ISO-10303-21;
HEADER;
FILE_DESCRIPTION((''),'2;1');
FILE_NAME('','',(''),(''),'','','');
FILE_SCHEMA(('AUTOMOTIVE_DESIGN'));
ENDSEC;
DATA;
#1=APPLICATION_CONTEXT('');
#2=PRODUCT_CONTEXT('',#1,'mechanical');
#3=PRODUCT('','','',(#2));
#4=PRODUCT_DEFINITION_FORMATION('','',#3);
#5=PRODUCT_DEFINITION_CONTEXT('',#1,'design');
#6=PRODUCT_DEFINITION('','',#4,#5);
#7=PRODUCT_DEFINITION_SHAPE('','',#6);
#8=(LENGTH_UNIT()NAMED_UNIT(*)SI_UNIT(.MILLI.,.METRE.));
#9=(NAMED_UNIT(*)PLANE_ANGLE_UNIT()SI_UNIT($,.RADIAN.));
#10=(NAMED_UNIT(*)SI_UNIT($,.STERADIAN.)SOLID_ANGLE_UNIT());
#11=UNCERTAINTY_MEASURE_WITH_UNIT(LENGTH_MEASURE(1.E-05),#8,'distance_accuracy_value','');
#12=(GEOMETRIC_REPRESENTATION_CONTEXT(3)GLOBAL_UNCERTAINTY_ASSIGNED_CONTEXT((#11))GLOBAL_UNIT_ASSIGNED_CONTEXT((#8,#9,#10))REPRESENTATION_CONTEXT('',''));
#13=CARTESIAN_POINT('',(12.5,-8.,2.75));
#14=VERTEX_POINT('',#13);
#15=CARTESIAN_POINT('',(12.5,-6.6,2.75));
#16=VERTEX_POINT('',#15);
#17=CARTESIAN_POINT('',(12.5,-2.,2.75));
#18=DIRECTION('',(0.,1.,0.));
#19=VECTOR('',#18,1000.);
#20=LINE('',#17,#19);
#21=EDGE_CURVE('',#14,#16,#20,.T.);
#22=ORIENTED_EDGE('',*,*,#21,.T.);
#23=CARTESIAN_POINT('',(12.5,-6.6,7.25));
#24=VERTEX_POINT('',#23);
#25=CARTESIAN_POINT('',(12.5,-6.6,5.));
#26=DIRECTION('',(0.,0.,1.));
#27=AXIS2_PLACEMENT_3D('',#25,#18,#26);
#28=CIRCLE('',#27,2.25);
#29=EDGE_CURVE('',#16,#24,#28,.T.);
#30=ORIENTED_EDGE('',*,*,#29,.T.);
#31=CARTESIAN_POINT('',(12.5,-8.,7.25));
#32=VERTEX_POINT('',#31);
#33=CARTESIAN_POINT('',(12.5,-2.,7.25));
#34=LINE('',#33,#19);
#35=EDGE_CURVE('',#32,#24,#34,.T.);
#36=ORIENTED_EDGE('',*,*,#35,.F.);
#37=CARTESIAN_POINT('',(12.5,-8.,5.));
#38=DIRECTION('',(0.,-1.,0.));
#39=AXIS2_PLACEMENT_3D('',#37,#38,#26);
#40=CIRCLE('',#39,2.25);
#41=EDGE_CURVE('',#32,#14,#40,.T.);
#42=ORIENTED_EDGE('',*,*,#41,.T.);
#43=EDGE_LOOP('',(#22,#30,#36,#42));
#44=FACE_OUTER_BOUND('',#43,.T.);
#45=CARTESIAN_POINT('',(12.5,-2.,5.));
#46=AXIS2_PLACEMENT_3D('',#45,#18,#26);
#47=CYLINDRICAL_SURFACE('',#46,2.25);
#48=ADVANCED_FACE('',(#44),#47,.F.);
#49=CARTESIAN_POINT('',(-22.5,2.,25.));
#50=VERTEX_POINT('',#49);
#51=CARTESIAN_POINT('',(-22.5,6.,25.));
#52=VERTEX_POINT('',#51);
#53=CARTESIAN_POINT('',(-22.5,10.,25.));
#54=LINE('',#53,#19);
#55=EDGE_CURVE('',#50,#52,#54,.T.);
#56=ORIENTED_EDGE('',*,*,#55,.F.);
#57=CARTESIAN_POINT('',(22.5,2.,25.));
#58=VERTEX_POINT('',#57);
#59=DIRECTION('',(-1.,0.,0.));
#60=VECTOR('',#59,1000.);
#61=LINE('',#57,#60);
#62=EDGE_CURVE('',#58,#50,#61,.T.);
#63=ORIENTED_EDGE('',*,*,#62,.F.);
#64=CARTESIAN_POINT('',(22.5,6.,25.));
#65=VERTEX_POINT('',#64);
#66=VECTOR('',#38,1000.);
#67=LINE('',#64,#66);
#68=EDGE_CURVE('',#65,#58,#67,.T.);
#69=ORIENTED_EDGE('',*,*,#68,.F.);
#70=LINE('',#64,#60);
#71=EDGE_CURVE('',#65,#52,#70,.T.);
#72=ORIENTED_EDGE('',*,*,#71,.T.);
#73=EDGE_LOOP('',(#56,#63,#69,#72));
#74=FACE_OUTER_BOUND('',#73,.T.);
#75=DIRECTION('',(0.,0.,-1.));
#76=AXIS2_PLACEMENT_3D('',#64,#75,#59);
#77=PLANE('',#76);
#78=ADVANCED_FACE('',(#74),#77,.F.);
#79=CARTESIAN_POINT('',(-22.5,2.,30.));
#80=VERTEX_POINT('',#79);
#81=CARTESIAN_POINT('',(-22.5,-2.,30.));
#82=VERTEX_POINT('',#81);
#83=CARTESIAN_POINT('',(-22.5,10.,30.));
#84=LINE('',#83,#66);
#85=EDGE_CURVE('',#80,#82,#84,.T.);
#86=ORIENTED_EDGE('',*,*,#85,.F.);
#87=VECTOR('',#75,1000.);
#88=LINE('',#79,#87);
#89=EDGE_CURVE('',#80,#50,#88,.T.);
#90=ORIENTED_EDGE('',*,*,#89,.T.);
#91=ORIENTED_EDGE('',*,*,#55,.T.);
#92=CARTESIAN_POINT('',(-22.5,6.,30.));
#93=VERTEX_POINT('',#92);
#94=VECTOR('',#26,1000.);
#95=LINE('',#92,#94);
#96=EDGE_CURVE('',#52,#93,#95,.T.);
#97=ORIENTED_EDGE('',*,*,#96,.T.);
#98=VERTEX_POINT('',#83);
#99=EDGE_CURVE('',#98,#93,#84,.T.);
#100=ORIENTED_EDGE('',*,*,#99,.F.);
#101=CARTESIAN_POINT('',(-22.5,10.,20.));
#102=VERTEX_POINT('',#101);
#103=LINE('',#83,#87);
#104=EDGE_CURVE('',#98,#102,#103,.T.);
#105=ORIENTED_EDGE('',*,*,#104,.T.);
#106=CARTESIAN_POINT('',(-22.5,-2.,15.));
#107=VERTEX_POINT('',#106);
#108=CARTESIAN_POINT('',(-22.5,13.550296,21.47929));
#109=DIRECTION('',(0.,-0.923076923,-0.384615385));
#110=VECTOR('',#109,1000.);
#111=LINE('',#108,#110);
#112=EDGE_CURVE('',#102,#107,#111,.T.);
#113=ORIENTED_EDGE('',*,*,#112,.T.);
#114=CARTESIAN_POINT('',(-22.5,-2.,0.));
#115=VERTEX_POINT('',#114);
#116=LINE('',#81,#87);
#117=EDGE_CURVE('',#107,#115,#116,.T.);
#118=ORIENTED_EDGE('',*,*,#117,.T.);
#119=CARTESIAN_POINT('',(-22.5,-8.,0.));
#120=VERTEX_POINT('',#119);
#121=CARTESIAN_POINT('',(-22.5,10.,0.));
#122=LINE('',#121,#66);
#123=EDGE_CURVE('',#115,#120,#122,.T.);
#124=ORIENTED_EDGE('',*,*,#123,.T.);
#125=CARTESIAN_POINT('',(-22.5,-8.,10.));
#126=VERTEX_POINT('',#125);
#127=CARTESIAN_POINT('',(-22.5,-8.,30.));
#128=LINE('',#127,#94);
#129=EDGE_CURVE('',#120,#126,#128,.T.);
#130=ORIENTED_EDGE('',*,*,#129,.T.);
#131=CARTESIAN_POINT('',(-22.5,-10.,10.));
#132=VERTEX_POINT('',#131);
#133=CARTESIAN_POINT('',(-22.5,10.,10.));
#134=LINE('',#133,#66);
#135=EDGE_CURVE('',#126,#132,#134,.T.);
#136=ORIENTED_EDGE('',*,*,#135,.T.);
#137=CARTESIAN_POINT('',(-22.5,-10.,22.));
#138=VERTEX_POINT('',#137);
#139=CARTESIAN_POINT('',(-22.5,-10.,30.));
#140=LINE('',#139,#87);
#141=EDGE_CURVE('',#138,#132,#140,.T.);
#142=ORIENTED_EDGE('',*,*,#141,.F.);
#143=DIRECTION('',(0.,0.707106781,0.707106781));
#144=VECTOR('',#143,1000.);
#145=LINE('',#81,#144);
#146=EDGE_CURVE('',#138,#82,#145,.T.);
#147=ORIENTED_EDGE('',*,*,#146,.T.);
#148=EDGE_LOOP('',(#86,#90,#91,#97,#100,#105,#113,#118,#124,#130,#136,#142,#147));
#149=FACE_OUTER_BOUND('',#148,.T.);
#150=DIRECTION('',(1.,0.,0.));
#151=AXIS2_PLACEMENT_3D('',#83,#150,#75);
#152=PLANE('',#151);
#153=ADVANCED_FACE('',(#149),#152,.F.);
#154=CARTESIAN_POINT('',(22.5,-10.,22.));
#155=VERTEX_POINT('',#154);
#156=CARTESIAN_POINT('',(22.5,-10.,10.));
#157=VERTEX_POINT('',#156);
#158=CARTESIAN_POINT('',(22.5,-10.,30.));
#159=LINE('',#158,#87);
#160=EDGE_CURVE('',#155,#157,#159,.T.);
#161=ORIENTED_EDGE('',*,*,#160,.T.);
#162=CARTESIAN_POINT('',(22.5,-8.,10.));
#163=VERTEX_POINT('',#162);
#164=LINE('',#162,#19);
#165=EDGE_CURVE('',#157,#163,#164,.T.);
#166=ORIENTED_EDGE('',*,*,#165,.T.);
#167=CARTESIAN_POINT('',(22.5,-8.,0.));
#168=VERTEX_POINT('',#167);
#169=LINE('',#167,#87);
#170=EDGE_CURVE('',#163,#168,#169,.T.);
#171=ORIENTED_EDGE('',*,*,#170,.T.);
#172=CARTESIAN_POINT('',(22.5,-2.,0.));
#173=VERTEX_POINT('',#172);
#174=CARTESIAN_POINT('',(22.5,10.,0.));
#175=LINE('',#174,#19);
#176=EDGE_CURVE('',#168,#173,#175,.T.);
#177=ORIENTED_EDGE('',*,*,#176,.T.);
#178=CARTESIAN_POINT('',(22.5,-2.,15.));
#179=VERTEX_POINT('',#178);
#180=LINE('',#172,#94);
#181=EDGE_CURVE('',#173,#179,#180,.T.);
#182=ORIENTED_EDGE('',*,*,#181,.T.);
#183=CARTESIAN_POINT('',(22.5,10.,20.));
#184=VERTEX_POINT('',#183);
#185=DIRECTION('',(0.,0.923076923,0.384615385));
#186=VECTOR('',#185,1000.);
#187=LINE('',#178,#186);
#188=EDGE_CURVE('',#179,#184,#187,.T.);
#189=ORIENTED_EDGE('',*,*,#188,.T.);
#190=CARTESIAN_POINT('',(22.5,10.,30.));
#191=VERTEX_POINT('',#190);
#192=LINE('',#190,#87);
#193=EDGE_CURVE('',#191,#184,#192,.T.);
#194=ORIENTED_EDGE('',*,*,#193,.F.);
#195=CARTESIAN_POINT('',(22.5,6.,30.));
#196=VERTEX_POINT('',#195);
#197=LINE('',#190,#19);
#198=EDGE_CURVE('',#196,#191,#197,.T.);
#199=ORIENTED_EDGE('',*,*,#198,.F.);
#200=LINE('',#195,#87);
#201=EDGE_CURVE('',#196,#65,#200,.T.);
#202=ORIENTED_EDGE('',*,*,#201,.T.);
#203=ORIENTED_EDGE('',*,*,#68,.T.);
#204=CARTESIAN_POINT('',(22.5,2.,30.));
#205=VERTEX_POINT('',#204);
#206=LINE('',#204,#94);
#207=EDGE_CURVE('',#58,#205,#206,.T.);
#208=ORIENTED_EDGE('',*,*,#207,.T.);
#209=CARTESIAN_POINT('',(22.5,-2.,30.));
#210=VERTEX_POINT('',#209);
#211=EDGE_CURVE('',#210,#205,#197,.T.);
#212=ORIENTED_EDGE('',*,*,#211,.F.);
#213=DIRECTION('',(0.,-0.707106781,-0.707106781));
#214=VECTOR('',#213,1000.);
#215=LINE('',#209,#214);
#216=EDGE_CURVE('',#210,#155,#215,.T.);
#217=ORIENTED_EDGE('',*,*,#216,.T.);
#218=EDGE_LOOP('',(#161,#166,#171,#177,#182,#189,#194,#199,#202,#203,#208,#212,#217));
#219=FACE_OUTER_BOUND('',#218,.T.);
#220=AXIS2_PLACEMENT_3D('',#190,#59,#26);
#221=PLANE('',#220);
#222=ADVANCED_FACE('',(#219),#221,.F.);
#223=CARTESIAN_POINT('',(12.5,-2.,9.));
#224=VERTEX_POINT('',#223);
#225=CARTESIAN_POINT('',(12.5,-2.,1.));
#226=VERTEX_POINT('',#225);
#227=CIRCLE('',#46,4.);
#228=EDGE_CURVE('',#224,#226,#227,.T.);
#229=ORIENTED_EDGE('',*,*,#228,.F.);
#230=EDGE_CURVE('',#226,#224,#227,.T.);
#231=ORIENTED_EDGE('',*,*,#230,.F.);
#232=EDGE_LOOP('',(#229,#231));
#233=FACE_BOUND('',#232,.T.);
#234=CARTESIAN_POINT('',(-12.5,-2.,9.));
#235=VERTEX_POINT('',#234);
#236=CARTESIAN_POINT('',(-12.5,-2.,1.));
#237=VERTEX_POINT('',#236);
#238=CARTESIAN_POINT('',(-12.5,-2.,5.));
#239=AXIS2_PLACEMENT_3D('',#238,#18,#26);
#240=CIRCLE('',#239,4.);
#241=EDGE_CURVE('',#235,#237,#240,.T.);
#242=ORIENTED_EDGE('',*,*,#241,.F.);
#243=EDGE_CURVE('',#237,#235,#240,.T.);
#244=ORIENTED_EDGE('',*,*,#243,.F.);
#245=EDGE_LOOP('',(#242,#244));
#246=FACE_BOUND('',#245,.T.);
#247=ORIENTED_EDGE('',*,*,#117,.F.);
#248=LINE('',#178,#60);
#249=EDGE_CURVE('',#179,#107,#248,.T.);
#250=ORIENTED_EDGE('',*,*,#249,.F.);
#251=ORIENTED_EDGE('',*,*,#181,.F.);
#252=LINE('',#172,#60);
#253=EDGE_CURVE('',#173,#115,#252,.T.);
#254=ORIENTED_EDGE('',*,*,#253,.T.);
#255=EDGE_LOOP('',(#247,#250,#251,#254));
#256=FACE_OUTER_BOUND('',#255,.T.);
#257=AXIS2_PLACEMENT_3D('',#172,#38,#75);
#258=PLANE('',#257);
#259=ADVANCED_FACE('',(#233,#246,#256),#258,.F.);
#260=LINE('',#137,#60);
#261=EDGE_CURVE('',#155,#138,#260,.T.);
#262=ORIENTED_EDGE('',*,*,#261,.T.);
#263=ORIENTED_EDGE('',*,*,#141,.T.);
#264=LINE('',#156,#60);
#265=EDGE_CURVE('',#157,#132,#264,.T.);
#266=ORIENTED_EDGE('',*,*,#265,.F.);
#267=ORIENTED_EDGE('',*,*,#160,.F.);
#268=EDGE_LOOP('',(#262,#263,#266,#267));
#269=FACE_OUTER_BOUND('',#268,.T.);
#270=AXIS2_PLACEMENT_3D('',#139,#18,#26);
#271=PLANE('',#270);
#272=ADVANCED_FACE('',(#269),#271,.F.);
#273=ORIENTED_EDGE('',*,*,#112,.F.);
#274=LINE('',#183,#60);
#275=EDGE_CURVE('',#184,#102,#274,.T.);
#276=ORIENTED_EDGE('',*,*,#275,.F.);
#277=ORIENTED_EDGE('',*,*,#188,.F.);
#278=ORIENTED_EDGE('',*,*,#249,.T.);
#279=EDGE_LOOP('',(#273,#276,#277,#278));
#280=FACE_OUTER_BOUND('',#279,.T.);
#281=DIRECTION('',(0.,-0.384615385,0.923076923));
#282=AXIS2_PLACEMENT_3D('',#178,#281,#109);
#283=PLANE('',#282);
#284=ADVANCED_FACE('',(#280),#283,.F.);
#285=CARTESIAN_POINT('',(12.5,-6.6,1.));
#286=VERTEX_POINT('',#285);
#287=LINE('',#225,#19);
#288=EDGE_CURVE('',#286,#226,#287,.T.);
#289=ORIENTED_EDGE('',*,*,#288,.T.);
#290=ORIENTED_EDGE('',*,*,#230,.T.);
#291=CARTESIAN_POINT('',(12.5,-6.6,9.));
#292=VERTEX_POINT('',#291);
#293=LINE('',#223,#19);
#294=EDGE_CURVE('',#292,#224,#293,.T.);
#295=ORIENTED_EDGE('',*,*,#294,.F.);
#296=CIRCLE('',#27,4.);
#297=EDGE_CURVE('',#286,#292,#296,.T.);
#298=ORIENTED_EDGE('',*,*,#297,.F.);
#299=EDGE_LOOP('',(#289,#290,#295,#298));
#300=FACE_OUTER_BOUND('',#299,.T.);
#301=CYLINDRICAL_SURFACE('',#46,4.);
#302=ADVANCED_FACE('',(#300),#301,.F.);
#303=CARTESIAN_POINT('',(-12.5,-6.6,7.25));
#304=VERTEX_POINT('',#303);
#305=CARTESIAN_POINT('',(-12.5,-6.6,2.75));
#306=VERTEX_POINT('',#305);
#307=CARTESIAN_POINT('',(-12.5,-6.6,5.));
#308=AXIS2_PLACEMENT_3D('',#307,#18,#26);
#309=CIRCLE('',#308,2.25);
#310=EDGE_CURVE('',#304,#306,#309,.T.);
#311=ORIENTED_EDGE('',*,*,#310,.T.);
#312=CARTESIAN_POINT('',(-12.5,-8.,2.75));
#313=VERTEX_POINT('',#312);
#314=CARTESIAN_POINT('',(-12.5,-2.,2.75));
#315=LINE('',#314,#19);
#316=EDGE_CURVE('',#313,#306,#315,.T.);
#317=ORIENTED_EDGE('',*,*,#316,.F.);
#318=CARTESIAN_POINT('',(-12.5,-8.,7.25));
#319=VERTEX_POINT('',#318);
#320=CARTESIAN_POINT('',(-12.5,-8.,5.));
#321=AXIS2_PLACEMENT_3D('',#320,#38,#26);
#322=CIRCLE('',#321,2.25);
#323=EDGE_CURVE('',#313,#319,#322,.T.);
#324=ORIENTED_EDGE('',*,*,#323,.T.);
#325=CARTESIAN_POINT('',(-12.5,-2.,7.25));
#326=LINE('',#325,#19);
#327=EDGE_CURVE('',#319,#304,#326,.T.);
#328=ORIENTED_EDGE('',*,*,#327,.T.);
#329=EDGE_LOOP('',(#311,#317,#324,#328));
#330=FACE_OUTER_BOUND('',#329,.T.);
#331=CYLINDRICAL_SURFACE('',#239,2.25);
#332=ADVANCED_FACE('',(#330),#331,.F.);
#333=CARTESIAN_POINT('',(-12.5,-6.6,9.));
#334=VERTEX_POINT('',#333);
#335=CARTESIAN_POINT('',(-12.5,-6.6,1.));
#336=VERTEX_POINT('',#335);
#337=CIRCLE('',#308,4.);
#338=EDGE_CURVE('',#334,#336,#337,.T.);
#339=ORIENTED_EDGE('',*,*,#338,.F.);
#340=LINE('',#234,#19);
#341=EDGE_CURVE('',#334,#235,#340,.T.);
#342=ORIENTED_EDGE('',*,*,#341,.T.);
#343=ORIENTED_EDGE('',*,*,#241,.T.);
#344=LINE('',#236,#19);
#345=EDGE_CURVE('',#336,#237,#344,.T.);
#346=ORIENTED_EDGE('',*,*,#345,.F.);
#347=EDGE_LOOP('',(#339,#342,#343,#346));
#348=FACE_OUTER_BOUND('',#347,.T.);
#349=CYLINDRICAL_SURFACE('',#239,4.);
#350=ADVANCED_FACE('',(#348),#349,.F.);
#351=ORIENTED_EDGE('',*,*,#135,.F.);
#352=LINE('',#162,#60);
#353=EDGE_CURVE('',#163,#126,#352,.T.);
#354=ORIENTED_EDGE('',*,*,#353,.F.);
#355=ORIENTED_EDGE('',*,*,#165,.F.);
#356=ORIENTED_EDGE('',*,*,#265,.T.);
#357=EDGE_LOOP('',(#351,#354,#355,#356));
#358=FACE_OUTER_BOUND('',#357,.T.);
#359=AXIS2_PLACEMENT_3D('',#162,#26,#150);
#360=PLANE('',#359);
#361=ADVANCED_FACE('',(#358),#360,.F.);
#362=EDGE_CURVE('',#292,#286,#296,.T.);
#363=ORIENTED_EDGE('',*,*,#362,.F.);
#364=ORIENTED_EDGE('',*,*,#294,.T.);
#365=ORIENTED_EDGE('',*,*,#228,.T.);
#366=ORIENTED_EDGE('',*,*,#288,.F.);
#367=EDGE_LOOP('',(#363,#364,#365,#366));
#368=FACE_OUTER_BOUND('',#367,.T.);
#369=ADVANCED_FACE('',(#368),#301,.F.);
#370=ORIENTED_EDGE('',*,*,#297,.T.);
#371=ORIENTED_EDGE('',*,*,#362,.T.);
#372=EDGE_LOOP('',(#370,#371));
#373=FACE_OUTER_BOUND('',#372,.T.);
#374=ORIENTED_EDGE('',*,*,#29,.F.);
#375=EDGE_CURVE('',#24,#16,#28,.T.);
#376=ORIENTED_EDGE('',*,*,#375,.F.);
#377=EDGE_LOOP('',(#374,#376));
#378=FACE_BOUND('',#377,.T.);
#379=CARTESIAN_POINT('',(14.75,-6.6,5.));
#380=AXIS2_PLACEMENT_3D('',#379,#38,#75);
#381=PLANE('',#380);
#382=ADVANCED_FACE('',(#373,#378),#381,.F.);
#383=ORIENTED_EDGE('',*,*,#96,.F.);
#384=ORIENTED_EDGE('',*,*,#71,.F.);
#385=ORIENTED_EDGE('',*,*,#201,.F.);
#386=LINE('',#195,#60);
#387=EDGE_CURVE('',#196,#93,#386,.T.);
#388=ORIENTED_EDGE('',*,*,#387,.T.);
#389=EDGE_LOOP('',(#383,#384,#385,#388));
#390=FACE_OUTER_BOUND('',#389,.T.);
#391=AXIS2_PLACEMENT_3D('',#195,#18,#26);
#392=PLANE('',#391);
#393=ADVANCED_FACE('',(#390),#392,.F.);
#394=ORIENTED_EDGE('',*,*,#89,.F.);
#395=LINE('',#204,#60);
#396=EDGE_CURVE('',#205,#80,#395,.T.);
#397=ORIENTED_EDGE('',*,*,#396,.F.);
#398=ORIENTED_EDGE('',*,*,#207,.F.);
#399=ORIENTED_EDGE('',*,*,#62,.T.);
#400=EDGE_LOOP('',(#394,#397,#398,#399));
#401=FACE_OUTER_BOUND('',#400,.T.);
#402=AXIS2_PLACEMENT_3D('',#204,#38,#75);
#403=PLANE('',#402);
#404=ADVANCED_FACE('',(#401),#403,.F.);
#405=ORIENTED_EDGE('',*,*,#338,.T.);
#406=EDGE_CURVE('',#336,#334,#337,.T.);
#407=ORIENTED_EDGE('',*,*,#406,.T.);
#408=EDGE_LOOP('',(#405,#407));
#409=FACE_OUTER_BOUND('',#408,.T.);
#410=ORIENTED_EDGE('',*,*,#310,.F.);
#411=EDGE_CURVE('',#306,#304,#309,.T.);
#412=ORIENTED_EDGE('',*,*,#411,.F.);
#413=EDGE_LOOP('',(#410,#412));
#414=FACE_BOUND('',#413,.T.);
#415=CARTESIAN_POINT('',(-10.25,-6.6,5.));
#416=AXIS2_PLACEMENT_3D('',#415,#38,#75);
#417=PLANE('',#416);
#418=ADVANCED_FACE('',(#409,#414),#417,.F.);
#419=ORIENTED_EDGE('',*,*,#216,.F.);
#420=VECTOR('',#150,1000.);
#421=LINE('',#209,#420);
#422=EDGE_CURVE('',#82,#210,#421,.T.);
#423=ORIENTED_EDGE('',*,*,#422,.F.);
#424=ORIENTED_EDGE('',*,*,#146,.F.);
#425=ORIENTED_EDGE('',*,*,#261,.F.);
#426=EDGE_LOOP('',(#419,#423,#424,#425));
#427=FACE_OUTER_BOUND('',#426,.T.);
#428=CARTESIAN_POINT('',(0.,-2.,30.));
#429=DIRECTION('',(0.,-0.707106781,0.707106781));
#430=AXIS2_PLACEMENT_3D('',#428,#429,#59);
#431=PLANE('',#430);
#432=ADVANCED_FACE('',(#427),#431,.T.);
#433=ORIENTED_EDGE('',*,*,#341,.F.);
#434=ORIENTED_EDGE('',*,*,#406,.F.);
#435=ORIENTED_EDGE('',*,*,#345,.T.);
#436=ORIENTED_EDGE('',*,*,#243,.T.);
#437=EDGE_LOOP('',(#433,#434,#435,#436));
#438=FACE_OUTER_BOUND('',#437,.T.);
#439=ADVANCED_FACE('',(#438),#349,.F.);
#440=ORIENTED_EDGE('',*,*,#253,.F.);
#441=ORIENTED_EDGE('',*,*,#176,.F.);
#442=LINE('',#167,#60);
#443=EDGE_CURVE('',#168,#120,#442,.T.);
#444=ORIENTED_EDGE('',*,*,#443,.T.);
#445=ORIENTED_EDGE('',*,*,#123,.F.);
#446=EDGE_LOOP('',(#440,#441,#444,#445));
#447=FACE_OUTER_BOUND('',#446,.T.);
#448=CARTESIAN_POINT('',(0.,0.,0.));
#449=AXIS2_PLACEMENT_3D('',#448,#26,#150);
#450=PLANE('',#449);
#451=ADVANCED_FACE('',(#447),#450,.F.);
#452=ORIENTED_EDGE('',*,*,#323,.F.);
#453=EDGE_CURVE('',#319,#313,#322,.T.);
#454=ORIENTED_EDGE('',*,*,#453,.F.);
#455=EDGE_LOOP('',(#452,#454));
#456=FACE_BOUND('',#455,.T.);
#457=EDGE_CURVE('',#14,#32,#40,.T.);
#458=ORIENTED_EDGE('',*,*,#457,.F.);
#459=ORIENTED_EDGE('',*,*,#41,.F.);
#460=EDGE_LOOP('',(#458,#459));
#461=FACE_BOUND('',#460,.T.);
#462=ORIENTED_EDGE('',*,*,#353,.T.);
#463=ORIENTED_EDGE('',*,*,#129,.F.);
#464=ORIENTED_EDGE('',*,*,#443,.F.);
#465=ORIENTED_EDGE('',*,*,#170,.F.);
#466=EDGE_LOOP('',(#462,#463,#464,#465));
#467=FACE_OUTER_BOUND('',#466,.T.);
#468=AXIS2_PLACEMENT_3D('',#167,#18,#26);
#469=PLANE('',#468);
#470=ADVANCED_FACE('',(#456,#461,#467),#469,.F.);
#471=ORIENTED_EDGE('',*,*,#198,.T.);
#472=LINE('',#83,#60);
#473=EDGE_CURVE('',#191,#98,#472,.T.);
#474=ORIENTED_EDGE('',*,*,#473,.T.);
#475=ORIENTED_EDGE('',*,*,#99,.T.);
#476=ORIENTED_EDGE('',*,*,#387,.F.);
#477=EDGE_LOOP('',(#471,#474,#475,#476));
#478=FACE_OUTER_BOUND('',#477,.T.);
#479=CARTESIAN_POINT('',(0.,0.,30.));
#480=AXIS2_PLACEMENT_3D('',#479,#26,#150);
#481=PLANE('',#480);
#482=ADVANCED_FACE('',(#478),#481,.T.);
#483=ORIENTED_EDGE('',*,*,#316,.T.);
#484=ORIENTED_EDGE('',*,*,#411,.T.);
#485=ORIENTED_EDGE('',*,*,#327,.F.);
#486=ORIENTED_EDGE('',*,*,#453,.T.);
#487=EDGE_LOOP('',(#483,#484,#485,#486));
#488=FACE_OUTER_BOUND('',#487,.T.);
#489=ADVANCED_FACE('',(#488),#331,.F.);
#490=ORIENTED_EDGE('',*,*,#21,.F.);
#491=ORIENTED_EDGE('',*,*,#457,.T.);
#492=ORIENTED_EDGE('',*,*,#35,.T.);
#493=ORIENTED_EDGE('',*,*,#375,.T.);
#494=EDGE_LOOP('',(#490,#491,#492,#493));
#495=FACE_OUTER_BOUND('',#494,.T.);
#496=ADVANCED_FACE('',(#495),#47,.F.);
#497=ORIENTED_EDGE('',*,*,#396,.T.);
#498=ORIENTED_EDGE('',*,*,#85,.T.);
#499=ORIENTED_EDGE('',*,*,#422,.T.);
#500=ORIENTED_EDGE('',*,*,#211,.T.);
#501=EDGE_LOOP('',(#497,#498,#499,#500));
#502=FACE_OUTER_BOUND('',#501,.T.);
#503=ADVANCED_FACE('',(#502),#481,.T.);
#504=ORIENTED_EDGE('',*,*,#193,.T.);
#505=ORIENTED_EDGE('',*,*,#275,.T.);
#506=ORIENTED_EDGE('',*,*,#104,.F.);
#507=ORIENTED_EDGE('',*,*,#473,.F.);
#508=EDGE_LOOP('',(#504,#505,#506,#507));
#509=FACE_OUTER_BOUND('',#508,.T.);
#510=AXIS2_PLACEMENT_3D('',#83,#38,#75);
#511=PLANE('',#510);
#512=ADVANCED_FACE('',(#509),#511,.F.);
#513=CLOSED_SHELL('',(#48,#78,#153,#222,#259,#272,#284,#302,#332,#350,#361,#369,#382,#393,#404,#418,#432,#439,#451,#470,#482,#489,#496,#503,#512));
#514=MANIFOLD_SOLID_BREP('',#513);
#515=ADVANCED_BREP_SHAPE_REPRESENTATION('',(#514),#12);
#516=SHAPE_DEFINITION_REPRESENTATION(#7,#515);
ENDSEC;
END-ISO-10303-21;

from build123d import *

# Parameters (mm, degrees)
SKETCH1_W                                        = 45
SKETCH1_H                                        = 20
BOSS_EXTRUDE1_DEPTH                              = 30
CUT_EXTRUDE1_DEPTH                               = 56
CUT_EXTRUDE1_DEPTH_BACK                          = 56
SKETCH2_W                                        = 5
SKETCH2_H                                        = 4
CHAMFER1_SIZE                                    = 8
HOLE_FOR_SOCKET_HEAD_CAP_SCREW_TYPE1_D           = 4.5
HOLE_FOR_SOCKET_HEAD_CAP_SCREW_TYPE1_CBORE_D     = 8
HOLE_FOR_SOCKET_HEAD_CAP_SCREW_TYPE1_CBORE_DEPTH = 4.6
CUT_EXTRUDE2_DEPTH                               = 56
CUT_EXTRUDE2_DEPTH_BACK                          = 56
SKETCH7_W                                        = 10
SKETCH7_H                                        = 2


with BuildPart() as part:
    # Sketch1 → Boss-Extrude1 (new body)
    with BuildSketch(Plane.XY):
        Rectangle(SKETCH1_W, SKETCH1_H)
    extrude(amount=BOSS_EXTRUDE1_DEPTH)

    # Sketch2 → Cut-Extrude1 (cut, two sides: drawn at the far end of the back side and taken through both)
    with BuildSketch(Plane.ZY.offset(22.5).offset(-CUT_EXTRUDE1_DEPTH_BACK)):
        Polygon((0, -2), (15, -2), (20, 10), (0, 10), align=None)
        with Locations((27.5, 4)):
            Rectangle(SKETCH2_W, SKETCH2_H)
    extrude(amount=CUT_EXTRUDE1_DEPTH + CUT_EXTRUDE1_DEPTH_BACK, mode=Mode.SUBTRACT)

    # Chamfer1
    chamfer1_edges = [part.edges().sort_by_distance(p)[0] for p in [
        (0, -10, 30),
    ]]
    chamfer(chamfer1_edges, length=CHAMFER1_SIZE)

    # Hole for socket head cap screw, type1 (through all)
    with Locations(Plane(origin=(0, -2, 0), x_dir=(1, 0, 0), z_dir=(0, 1, 0))):
        with Locations((-12.5, -5), (12.5, -5)):
            CounterBoreHole(HOLE_FOR_SOCKET_HEAD_CAP_SCREW_TYPE1_D / 2, HOLE_FOR_SOCKET_HEAD_CAP_SCREW_TYPE1_CBORE_D / 2, HOLE_FOR_SOCKET_HEAD_CAP_SCREW_TYPE1_CBORE_DEPTH)

    # Sketch7 → Cut-Extrude2 (cut, two sides: drawn at the far end of the back side and taken through both)
    with BuildSketch(Plane.ZY.offset(22.5).offset(-CUT_EXTRUDE2_DEPTH_BACK)):
        with Locations((5, -9)):
            Rectangle(SKETCH7_W, SKETCH7_H)
    extrude(amount=CUT_EXTRUDE2_DEPTH + CUT_EXTRUDE2_DEPTH_BACK, mode=Mode.SUBTRACT)


solid = part.part
